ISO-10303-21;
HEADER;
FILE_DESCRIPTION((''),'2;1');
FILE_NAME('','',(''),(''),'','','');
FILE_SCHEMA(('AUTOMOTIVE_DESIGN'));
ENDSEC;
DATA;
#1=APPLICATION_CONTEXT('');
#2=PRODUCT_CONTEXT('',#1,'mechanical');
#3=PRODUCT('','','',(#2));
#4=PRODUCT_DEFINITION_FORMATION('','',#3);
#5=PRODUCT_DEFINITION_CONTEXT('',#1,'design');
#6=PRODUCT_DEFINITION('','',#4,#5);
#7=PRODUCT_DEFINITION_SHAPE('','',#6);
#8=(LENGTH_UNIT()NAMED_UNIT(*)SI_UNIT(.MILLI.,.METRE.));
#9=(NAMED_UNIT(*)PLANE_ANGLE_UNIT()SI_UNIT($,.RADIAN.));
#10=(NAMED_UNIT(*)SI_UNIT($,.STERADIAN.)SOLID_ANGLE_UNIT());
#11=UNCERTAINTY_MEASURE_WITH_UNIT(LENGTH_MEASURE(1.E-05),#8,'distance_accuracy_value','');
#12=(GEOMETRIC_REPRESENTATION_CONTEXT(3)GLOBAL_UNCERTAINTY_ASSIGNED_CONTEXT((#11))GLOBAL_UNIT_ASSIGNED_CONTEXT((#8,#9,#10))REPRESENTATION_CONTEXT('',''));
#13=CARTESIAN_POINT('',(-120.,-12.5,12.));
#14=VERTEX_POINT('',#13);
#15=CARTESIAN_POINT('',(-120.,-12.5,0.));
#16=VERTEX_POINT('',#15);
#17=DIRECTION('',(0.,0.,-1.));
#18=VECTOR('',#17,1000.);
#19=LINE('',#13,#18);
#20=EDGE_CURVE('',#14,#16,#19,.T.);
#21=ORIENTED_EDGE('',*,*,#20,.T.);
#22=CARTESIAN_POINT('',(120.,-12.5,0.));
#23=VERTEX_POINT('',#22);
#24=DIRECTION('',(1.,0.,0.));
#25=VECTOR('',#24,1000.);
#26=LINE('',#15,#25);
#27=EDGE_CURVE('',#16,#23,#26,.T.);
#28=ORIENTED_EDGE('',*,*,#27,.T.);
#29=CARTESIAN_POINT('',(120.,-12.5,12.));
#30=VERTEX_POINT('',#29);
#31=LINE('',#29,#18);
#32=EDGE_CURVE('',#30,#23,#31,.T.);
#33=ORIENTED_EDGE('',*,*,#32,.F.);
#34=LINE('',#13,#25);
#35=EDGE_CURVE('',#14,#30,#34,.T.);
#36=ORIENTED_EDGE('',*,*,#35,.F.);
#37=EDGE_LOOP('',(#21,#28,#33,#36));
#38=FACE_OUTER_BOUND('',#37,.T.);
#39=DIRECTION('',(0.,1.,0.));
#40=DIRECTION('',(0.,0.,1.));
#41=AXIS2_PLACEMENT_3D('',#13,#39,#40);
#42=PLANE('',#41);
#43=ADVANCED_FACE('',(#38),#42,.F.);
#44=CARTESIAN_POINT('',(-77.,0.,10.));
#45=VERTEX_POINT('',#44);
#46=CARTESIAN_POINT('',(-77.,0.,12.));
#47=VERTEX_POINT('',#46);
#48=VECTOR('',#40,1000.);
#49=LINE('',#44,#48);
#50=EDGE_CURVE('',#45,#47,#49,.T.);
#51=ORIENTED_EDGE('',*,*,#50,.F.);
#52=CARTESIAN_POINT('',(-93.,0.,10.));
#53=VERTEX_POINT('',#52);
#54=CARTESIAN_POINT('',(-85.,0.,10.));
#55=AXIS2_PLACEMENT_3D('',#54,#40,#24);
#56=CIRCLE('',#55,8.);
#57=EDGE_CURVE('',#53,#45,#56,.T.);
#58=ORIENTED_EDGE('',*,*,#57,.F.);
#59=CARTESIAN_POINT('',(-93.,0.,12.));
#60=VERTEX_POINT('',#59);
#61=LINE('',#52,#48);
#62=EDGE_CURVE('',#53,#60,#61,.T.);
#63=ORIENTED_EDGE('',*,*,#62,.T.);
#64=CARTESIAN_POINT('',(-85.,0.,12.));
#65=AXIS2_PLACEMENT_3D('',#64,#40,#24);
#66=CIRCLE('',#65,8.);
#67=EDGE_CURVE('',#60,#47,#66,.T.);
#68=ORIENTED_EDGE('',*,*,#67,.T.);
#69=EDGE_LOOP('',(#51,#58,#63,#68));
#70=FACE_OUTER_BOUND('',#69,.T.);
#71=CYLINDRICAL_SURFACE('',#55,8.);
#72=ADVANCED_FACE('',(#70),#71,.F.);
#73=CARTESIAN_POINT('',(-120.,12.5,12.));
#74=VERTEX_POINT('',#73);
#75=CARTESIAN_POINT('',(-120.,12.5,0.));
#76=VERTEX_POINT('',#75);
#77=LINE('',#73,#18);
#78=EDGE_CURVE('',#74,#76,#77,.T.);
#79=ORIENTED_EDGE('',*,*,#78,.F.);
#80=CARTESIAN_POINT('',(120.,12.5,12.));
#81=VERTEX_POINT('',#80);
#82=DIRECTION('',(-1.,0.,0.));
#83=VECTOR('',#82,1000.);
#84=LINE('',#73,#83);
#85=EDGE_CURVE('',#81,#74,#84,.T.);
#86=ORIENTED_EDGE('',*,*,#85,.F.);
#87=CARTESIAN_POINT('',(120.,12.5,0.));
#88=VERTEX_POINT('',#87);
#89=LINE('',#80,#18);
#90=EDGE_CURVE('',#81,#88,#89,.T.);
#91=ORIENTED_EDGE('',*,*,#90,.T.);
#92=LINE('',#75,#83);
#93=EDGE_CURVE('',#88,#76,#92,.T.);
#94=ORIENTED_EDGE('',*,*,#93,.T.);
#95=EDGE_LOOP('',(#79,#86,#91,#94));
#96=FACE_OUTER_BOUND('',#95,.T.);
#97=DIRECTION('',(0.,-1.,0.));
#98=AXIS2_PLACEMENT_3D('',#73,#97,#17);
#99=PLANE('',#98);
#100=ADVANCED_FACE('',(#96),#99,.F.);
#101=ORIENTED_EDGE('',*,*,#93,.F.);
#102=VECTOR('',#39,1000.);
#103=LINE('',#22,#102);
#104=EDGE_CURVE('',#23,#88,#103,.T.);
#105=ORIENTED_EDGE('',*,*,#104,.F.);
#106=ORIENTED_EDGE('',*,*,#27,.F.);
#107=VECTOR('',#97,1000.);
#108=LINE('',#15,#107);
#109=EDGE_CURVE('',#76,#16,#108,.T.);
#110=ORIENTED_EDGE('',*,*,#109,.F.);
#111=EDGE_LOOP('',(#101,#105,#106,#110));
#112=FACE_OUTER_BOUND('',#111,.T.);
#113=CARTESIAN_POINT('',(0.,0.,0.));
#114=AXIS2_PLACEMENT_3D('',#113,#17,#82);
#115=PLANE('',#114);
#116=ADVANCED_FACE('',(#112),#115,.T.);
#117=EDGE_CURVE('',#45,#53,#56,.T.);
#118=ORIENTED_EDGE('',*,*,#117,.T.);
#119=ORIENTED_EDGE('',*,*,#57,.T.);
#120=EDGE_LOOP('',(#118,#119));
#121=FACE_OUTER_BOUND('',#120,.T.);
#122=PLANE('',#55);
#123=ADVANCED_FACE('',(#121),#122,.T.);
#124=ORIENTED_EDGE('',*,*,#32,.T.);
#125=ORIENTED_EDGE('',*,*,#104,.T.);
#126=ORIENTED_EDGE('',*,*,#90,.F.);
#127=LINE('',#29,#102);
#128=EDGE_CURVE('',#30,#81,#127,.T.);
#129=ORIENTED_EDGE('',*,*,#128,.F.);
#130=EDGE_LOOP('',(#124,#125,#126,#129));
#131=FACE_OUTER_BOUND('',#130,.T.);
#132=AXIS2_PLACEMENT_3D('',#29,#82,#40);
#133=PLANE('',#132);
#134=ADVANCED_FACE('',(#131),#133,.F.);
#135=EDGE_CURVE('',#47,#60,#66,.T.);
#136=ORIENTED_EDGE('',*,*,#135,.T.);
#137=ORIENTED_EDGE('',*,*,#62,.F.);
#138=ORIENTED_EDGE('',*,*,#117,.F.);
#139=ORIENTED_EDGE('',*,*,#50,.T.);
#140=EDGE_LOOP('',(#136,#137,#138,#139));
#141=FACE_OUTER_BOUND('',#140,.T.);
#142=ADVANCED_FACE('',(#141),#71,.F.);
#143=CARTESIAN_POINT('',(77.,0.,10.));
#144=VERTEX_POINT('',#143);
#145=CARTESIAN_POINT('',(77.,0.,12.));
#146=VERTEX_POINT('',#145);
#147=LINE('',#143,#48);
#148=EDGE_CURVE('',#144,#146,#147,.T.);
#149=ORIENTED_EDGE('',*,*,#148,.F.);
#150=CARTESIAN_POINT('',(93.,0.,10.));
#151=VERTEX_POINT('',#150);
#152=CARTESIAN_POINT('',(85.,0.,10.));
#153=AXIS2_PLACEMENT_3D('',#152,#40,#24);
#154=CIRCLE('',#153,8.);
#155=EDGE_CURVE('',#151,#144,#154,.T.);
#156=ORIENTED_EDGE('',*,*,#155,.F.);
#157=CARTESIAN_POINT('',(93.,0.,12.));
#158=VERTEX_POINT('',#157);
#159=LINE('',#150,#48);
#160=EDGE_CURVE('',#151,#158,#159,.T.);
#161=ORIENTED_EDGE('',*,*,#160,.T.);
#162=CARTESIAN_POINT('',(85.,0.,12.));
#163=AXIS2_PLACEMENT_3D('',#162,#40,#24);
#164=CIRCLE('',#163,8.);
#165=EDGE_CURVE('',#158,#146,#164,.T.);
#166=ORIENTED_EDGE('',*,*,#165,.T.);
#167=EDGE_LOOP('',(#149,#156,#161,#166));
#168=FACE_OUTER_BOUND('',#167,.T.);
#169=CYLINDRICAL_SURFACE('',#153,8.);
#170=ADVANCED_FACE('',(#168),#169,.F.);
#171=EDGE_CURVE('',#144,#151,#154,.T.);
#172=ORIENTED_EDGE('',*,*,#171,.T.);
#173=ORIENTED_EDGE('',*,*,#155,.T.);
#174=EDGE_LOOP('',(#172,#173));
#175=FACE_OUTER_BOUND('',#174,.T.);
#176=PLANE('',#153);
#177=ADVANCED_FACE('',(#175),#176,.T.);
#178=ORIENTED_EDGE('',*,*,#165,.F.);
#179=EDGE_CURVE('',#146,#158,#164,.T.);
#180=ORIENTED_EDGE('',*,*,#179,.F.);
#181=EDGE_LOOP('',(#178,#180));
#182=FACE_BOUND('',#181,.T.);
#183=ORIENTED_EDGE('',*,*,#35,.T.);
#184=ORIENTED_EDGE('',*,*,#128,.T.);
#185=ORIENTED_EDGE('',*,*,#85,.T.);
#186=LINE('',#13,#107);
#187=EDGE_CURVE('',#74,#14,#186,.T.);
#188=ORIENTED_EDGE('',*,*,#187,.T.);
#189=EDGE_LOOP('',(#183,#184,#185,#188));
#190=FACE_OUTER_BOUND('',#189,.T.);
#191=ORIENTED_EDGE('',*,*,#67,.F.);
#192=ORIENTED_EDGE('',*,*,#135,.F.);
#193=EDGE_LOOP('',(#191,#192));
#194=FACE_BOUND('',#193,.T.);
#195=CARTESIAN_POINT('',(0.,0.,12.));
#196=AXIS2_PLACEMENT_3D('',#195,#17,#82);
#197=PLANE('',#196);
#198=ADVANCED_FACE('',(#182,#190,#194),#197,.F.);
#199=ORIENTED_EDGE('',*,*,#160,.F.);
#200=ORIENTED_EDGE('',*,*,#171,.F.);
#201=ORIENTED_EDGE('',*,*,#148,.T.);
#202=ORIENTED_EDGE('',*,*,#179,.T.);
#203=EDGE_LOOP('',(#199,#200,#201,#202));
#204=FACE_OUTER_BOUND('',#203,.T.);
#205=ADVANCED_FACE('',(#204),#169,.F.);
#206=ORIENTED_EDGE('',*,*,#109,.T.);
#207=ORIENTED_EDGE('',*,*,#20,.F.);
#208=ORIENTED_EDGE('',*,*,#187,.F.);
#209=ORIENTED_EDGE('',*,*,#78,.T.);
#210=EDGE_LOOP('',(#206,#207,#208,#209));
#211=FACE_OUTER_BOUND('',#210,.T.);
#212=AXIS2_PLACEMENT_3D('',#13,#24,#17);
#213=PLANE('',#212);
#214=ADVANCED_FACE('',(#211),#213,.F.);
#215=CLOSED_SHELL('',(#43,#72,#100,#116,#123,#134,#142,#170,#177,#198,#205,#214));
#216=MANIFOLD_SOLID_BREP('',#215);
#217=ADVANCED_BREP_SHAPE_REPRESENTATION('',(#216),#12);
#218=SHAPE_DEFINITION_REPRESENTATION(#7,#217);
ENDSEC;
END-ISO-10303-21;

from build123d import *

# Parameters (mm, degrees)
SKETCH_1_W          = 240
SKETCH_1_H          = 25
EXTRUDE_1_DEPTH     = 12
SKETCH_2_R          = 8
CUT_EXTRUDE_1_DEPTH = 2


with BuildPart() as part:
    # 草图1 → 凸台-拉伸1 (new body)
    with BuildSketch(Plane.XY):
        Rectangle(SKETCH_1_W, SKETCH_1_H)
    extrude(amount=EXTRUDE_1_DEPTH)

    # 草图2 → 切除-拉伸1 (cut)
    with BuildSketch(Plane.XY.offset(12)):
        with Locations((85, 0)):
            Circle(SKETCH_2_R)
        with Locations((-85, 0)):
            Circle(SKETCH_2_R)
    extrude(amount=-CUT_EXTRUDE_1_DEPTH, mode=Mode.SUBTRACT)


solid = part.part
